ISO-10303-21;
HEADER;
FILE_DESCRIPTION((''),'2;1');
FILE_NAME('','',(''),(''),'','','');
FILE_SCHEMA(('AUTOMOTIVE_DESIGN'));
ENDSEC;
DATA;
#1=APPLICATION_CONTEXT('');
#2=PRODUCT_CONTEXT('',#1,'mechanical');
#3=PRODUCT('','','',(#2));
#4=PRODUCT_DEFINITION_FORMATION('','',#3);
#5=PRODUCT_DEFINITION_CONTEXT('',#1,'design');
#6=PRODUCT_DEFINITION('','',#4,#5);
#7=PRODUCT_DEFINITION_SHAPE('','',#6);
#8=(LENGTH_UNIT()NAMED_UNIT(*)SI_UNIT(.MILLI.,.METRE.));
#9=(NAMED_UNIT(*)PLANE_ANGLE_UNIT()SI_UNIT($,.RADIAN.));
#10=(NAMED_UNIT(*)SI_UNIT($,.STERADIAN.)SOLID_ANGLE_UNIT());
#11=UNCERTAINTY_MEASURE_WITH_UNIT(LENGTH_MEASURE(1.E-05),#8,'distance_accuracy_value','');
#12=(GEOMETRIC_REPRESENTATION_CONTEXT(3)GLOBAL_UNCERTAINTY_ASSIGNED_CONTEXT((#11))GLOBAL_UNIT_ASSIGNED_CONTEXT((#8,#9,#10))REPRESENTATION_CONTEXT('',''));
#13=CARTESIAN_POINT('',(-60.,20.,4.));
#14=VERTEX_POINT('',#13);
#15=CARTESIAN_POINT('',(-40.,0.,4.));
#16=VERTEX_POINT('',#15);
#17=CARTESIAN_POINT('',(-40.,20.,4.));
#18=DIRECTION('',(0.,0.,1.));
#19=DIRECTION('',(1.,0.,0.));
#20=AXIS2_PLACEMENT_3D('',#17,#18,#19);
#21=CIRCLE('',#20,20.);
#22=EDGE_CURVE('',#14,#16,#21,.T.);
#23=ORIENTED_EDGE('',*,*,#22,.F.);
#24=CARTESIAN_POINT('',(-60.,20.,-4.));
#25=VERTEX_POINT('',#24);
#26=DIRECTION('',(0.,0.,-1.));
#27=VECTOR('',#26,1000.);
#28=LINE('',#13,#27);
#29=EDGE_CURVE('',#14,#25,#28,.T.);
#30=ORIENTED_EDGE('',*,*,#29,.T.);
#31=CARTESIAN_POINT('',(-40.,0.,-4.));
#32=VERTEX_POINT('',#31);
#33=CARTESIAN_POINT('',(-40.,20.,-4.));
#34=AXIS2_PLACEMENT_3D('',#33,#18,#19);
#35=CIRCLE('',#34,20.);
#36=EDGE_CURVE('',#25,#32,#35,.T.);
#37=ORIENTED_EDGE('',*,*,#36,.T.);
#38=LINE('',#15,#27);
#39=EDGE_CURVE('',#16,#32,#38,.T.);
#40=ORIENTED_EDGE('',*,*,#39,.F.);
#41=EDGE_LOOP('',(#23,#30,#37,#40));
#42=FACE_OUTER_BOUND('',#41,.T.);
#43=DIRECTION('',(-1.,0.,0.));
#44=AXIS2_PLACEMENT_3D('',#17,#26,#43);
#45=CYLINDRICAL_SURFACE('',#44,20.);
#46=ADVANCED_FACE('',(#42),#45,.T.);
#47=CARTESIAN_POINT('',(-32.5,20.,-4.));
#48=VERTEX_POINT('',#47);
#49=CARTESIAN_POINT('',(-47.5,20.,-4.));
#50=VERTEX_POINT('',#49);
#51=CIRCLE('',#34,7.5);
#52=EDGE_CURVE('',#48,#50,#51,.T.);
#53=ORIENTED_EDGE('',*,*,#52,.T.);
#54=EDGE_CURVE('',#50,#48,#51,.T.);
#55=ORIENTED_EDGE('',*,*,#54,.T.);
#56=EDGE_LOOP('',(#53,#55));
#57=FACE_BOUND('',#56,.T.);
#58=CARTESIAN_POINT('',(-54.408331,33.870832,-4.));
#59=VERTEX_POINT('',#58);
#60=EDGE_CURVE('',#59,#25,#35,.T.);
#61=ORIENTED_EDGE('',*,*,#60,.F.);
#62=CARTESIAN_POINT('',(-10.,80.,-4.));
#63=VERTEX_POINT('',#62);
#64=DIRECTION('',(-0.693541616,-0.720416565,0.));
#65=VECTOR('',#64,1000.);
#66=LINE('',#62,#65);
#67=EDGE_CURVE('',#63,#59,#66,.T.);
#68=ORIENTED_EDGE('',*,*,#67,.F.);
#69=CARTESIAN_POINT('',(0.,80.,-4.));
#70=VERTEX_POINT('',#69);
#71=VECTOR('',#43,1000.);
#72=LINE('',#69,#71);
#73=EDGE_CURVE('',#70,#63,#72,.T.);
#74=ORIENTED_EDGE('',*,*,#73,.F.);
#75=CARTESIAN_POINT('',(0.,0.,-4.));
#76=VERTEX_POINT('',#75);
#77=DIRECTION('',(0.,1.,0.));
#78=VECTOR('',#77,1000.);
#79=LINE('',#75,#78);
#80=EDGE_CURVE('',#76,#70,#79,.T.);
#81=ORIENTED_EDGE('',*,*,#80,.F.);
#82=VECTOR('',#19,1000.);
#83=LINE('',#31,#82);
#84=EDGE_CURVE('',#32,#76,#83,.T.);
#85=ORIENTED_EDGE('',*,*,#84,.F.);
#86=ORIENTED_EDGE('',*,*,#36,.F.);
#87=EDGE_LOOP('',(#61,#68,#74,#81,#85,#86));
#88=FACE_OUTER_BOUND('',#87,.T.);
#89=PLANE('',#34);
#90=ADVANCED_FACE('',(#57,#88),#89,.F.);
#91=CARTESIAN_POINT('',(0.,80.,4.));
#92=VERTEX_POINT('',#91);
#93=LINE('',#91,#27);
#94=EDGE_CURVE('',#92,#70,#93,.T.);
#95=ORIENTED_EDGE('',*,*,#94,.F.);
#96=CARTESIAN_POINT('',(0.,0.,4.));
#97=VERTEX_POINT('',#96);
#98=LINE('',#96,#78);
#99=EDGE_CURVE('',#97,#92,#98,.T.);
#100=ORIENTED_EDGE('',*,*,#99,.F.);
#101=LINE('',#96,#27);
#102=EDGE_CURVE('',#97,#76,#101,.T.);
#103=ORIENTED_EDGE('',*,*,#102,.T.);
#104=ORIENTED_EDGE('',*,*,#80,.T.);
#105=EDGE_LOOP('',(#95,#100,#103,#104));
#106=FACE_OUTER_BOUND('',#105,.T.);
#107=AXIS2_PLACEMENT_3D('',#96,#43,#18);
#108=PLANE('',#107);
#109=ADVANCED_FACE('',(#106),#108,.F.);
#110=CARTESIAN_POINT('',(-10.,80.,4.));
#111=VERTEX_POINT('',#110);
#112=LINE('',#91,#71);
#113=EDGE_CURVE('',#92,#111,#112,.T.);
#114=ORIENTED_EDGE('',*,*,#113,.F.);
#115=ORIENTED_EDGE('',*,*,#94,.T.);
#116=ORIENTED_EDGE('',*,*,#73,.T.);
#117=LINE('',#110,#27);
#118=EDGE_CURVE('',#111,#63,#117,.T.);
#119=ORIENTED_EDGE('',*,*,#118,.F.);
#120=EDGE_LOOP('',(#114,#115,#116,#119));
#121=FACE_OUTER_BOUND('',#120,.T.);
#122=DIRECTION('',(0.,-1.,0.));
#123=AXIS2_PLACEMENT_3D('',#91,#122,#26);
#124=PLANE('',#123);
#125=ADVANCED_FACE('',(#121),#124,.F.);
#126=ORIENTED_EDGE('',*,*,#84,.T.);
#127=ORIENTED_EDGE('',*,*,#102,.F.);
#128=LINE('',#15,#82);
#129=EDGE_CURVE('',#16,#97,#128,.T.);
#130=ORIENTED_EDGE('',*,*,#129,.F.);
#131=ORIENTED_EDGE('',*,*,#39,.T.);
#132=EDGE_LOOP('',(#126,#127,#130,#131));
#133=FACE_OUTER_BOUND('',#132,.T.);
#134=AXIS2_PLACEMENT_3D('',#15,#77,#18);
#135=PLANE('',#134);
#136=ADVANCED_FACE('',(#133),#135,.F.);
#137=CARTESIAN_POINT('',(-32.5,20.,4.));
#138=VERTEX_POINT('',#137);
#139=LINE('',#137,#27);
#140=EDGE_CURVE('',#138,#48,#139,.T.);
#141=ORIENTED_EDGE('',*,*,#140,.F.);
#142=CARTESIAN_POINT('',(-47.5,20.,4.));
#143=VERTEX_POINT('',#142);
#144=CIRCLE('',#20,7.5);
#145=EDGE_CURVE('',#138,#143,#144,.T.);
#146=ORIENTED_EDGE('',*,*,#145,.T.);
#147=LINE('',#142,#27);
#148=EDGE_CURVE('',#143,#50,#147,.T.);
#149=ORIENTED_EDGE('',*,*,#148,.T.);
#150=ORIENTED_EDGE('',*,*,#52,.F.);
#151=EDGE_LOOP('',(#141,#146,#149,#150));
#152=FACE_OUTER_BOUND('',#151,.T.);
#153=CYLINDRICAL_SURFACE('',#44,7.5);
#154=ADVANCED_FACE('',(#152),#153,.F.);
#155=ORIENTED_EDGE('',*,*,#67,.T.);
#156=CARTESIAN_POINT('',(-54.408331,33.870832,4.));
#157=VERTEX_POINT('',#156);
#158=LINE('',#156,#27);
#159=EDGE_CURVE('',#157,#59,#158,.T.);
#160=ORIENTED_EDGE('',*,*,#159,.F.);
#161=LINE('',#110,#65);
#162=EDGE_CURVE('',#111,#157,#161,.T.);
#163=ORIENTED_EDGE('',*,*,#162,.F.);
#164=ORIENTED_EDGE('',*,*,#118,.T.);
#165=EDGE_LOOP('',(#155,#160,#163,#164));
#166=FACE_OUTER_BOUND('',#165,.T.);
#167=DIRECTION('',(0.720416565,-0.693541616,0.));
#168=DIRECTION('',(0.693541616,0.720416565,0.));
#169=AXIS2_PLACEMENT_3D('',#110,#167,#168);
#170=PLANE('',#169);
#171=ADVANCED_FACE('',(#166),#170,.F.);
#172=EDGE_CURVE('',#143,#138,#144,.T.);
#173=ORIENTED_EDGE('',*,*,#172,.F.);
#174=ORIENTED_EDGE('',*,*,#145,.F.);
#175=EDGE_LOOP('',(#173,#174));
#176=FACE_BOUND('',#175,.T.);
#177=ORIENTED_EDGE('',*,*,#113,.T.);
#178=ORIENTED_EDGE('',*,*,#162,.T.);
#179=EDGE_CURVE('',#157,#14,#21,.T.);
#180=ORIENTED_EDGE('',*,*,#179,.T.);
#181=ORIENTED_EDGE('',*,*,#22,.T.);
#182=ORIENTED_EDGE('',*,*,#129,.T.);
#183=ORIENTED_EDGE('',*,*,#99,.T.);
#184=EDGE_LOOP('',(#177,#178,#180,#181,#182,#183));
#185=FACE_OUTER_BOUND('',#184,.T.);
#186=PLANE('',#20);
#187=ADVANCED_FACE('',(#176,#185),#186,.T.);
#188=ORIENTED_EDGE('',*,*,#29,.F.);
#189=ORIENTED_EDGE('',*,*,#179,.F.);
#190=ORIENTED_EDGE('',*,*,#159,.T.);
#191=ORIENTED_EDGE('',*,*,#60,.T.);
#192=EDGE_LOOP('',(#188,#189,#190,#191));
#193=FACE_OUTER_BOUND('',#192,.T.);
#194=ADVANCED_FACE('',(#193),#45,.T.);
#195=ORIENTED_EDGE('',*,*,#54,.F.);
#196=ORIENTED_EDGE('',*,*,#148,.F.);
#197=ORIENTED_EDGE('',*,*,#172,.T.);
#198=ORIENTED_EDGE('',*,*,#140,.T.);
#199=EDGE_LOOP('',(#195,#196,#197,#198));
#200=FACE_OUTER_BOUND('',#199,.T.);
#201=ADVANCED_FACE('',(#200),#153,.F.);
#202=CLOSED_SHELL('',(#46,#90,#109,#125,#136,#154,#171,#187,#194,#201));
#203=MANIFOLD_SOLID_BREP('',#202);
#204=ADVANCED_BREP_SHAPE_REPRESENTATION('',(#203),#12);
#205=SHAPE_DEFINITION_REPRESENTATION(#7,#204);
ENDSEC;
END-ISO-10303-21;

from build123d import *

# Parameters (mm, degrees)
SKETCH1_R           = 7.5
BOSS_EXTRUDE1_DEPTH = 4


with BuildPart() as part:
    # Sketch1 → Boss-Extrude1 (new, symmetric)
    with BuildSketch(Plane.XY):
        with BuildLine():
            Line((0, 0), (0, 80))
            Line((0, 80), (-10, 80))
            Line((-10, 80), (-54.4083313, 33.870832317))
            ThreePointArc((-54.4083313, 33.870832317), (-58.404030079, 12.171099896), (-40, 0))
            Line((-40, 0), (0, 0))
        make_face()
        with Locations((-40, 20)):
            Circle(SKETCH1_R, mode=Mode.SUBTRACT)
    extrude(amount=BOSS_EXTRUDE1_DEPTH, both=True)


solid = part.part
